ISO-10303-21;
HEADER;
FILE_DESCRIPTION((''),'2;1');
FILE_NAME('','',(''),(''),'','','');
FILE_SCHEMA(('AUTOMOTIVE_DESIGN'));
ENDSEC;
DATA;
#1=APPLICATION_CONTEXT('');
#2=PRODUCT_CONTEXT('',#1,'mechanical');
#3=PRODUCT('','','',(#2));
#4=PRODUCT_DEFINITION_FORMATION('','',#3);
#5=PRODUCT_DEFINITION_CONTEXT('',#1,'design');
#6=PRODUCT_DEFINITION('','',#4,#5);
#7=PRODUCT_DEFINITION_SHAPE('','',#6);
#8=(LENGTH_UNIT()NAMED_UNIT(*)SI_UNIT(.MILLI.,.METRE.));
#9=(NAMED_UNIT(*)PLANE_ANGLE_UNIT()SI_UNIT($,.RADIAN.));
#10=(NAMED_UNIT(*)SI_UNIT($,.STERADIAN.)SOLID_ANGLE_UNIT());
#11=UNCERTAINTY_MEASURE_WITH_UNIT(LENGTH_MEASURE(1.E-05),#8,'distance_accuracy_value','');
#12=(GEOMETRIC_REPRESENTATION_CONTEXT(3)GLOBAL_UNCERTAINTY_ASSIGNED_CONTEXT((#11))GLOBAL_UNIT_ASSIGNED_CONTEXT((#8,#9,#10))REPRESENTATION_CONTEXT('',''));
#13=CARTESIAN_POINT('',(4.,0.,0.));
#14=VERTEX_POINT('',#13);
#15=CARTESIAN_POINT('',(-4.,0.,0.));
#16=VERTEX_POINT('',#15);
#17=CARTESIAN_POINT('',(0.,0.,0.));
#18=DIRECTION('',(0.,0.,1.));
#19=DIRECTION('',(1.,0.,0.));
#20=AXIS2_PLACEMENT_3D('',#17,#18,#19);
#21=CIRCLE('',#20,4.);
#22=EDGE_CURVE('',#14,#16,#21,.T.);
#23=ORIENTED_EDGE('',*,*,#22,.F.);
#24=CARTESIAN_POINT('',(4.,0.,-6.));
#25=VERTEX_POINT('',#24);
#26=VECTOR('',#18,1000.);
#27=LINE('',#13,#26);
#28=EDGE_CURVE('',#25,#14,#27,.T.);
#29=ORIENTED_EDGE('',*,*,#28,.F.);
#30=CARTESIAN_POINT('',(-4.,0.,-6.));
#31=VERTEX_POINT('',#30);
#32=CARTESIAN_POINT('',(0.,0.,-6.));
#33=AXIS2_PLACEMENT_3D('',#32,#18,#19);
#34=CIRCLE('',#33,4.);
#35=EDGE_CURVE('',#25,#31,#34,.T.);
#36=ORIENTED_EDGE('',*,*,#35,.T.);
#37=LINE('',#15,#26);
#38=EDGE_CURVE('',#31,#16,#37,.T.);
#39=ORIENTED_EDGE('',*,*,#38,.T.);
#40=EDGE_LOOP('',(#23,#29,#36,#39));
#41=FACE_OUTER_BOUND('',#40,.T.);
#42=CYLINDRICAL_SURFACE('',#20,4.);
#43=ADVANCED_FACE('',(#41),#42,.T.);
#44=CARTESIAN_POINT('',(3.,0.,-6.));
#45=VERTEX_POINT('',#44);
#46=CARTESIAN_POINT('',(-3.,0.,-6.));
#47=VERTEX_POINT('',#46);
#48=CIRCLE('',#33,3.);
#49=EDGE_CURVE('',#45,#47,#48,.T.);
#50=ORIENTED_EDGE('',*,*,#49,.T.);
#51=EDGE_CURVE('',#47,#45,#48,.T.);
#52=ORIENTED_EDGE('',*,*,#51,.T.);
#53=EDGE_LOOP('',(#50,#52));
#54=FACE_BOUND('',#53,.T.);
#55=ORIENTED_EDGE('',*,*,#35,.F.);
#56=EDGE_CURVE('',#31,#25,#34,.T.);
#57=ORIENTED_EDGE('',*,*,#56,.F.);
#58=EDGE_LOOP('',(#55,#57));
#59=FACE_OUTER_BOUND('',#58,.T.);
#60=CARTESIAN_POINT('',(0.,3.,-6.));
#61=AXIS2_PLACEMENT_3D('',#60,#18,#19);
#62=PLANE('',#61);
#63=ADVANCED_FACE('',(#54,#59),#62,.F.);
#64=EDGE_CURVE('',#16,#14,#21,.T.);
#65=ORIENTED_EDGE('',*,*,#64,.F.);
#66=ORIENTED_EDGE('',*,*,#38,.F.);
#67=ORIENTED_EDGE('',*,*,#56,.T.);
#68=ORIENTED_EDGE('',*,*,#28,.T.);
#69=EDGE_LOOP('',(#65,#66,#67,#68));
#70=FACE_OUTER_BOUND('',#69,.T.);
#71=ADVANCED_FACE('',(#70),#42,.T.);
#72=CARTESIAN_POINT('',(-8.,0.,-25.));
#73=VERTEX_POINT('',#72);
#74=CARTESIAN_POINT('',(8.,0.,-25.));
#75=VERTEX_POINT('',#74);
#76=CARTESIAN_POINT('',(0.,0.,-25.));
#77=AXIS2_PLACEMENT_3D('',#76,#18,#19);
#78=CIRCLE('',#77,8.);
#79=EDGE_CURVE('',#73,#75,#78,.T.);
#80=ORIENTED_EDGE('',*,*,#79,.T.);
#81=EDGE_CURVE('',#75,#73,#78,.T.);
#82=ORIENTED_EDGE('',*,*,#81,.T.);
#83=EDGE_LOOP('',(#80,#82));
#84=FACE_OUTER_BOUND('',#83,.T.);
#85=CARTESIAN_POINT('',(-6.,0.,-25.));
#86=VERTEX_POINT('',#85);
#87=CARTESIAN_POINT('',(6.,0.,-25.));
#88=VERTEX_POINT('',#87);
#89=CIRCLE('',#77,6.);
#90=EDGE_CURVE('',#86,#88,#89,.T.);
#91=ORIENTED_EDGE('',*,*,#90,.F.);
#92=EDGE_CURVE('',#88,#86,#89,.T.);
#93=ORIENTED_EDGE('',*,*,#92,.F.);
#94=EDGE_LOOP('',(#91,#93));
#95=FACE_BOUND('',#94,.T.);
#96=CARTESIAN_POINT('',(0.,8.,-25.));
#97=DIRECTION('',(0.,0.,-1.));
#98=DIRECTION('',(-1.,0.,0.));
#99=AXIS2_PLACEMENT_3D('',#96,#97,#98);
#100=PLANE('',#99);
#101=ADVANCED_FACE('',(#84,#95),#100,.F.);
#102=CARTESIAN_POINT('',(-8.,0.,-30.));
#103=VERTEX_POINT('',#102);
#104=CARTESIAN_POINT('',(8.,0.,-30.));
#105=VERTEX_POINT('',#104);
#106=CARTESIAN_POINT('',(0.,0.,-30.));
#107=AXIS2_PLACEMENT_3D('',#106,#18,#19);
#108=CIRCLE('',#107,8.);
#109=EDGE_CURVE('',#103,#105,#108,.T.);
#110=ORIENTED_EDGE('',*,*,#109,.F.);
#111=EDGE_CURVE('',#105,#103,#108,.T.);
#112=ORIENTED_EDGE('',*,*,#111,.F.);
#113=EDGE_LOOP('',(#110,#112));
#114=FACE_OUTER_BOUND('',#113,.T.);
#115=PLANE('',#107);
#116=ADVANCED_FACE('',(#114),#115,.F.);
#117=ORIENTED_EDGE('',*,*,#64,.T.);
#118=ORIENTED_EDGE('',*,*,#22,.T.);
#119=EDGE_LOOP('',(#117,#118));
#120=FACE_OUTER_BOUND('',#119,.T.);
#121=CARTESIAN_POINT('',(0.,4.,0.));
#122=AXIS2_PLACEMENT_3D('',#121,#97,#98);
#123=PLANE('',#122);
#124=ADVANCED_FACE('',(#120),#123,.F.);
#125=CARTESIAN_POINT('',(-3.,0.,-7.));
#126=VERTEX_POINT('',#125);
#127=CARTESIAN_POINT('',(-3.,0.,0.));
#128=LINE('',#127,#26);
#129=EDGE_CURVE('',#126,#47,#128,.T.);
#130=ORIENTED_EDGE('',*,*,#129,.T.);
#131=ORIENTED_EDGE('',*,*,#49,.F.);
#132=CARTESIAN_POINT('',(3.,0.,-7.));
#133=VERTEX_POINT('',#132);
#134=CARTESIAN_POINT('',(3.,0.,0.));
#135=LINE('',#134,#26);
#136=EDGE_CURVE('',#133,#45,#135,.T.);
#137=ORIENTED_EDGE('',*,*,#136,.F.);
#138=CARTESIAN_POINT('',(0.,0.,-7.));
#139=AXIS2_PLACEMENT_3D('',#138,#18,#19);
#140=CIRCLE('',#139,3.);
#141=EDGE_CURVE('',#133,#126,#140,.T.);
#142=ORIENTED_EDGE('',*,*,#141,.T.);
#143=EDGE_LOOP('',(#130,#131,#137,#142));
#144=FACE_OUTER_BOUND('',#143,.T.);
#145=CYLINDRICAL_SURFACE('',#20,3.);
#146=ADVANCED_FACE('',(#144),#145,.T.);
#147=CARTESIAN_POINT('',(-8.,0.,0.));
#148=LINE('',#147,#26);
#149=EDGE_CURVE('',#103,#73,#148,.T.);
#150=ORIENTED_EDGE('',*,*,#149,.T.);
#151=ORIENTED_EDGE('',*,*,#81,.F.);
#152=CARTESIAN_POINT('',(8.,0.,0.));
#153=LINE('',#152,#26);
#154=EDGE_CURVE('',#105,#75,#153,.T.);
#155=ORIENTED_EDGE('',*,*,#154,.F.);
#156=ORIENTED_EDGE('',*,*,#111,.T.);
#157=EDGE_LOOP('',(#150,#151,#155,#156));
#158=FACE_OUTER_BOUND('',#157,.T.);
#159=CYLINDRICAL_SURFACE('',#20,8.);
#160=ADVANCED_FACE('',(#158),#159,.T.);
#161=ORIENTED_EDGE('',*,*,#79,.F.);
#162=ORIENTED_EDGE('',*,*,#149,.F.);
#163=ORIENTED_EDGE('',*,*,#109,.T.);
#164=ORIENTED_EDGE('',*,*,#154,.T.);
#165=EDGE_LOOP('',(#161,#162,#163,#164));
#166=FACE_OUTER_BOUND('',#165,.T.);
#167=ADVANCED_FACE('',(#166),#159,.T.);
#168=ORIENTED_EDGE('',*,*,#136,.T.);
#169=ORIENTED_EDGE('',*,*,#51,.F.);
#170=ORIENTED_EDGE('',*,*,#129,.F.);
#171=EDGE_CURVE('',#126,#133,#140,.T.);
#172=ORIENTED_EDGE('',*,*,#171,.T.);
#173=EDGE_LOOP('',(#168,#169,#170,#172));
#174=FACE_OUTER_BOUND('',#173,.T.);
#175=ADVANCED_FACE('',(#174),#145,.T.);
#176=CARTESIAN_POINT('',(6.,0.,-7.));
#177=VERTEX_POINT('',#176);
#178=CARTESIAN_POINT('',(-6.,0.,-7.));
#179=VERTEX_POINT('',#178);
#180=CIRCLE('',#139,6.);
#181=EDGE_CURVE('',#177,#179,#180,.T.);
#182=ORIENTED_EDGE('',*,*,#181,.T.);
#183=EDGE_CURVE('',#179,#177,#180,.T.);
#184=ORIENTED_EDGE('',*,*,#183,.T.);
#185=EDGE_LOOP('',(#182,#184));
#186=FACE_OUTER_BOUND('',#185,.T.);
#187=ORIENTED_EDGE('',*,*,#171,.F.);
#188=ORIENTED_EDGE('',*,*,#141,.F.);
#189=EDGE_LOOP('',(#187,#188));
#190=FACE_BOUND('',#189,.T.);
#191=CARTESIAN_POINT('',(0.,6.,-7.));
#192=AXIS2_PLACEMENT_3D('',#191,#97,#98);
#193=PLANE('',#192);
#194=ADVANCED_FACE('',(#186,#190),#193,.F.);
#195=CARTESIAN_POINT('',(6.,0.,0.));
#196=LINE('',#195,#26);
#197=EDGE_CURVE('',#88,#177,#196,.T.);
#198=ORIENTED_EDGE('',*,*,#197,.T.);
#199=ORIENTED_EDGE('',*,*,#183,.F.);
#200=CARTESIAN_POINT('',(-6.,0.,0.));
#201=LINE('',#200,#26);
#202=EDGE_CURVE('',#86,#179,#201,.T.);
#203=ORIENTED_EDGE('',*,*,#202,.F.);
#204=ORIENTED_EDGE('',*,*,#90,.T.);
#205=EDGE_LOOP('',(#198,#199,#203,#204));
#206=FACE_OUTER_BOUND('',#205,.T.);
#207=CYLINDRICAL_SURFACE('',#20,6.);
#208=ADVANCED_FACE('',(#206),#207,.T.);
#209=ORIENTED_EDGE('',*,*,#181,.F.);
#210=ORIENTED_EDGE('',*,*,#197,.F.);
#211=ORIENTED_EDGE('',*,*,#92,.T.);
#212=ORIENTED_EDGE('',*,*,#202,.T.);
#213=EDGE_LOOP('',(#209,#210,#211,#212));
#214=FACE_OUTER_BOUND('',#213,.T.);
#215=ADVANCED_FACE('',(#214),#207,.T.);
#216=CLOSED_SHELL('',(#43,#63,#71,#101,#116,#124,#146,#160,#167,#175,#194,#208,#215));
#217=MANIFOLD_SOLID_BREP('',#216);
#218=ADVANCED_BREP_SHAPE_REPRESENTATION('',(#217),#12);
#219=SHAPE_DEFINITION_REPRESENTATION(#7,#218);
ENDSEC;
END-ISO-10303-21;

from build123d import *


with BuildPart() as part:
    # Sketch1 → Revolve1 (revolve)
    with BuildSketch(Plane(origin=(0, 0, 0), x_dir=(0, 0, -1), z_dir=(1, 0, 0)), mode=Mode.PRIVATE) as revolve1_sk:
        Polygon((30, 0), (30, 8), (25, 8), (25, 6), (7, 6), (7, 3), (6, 3), (6, 4), (0, 4), (0, 0), align=None)
    revolve(revolve1_sk.sketch.rotate(Axis((0, 0, 0), (0, 0, -1)), 90), axis=Axis((0, 0, 0), (0, 0, -1)))


solid = part.part
